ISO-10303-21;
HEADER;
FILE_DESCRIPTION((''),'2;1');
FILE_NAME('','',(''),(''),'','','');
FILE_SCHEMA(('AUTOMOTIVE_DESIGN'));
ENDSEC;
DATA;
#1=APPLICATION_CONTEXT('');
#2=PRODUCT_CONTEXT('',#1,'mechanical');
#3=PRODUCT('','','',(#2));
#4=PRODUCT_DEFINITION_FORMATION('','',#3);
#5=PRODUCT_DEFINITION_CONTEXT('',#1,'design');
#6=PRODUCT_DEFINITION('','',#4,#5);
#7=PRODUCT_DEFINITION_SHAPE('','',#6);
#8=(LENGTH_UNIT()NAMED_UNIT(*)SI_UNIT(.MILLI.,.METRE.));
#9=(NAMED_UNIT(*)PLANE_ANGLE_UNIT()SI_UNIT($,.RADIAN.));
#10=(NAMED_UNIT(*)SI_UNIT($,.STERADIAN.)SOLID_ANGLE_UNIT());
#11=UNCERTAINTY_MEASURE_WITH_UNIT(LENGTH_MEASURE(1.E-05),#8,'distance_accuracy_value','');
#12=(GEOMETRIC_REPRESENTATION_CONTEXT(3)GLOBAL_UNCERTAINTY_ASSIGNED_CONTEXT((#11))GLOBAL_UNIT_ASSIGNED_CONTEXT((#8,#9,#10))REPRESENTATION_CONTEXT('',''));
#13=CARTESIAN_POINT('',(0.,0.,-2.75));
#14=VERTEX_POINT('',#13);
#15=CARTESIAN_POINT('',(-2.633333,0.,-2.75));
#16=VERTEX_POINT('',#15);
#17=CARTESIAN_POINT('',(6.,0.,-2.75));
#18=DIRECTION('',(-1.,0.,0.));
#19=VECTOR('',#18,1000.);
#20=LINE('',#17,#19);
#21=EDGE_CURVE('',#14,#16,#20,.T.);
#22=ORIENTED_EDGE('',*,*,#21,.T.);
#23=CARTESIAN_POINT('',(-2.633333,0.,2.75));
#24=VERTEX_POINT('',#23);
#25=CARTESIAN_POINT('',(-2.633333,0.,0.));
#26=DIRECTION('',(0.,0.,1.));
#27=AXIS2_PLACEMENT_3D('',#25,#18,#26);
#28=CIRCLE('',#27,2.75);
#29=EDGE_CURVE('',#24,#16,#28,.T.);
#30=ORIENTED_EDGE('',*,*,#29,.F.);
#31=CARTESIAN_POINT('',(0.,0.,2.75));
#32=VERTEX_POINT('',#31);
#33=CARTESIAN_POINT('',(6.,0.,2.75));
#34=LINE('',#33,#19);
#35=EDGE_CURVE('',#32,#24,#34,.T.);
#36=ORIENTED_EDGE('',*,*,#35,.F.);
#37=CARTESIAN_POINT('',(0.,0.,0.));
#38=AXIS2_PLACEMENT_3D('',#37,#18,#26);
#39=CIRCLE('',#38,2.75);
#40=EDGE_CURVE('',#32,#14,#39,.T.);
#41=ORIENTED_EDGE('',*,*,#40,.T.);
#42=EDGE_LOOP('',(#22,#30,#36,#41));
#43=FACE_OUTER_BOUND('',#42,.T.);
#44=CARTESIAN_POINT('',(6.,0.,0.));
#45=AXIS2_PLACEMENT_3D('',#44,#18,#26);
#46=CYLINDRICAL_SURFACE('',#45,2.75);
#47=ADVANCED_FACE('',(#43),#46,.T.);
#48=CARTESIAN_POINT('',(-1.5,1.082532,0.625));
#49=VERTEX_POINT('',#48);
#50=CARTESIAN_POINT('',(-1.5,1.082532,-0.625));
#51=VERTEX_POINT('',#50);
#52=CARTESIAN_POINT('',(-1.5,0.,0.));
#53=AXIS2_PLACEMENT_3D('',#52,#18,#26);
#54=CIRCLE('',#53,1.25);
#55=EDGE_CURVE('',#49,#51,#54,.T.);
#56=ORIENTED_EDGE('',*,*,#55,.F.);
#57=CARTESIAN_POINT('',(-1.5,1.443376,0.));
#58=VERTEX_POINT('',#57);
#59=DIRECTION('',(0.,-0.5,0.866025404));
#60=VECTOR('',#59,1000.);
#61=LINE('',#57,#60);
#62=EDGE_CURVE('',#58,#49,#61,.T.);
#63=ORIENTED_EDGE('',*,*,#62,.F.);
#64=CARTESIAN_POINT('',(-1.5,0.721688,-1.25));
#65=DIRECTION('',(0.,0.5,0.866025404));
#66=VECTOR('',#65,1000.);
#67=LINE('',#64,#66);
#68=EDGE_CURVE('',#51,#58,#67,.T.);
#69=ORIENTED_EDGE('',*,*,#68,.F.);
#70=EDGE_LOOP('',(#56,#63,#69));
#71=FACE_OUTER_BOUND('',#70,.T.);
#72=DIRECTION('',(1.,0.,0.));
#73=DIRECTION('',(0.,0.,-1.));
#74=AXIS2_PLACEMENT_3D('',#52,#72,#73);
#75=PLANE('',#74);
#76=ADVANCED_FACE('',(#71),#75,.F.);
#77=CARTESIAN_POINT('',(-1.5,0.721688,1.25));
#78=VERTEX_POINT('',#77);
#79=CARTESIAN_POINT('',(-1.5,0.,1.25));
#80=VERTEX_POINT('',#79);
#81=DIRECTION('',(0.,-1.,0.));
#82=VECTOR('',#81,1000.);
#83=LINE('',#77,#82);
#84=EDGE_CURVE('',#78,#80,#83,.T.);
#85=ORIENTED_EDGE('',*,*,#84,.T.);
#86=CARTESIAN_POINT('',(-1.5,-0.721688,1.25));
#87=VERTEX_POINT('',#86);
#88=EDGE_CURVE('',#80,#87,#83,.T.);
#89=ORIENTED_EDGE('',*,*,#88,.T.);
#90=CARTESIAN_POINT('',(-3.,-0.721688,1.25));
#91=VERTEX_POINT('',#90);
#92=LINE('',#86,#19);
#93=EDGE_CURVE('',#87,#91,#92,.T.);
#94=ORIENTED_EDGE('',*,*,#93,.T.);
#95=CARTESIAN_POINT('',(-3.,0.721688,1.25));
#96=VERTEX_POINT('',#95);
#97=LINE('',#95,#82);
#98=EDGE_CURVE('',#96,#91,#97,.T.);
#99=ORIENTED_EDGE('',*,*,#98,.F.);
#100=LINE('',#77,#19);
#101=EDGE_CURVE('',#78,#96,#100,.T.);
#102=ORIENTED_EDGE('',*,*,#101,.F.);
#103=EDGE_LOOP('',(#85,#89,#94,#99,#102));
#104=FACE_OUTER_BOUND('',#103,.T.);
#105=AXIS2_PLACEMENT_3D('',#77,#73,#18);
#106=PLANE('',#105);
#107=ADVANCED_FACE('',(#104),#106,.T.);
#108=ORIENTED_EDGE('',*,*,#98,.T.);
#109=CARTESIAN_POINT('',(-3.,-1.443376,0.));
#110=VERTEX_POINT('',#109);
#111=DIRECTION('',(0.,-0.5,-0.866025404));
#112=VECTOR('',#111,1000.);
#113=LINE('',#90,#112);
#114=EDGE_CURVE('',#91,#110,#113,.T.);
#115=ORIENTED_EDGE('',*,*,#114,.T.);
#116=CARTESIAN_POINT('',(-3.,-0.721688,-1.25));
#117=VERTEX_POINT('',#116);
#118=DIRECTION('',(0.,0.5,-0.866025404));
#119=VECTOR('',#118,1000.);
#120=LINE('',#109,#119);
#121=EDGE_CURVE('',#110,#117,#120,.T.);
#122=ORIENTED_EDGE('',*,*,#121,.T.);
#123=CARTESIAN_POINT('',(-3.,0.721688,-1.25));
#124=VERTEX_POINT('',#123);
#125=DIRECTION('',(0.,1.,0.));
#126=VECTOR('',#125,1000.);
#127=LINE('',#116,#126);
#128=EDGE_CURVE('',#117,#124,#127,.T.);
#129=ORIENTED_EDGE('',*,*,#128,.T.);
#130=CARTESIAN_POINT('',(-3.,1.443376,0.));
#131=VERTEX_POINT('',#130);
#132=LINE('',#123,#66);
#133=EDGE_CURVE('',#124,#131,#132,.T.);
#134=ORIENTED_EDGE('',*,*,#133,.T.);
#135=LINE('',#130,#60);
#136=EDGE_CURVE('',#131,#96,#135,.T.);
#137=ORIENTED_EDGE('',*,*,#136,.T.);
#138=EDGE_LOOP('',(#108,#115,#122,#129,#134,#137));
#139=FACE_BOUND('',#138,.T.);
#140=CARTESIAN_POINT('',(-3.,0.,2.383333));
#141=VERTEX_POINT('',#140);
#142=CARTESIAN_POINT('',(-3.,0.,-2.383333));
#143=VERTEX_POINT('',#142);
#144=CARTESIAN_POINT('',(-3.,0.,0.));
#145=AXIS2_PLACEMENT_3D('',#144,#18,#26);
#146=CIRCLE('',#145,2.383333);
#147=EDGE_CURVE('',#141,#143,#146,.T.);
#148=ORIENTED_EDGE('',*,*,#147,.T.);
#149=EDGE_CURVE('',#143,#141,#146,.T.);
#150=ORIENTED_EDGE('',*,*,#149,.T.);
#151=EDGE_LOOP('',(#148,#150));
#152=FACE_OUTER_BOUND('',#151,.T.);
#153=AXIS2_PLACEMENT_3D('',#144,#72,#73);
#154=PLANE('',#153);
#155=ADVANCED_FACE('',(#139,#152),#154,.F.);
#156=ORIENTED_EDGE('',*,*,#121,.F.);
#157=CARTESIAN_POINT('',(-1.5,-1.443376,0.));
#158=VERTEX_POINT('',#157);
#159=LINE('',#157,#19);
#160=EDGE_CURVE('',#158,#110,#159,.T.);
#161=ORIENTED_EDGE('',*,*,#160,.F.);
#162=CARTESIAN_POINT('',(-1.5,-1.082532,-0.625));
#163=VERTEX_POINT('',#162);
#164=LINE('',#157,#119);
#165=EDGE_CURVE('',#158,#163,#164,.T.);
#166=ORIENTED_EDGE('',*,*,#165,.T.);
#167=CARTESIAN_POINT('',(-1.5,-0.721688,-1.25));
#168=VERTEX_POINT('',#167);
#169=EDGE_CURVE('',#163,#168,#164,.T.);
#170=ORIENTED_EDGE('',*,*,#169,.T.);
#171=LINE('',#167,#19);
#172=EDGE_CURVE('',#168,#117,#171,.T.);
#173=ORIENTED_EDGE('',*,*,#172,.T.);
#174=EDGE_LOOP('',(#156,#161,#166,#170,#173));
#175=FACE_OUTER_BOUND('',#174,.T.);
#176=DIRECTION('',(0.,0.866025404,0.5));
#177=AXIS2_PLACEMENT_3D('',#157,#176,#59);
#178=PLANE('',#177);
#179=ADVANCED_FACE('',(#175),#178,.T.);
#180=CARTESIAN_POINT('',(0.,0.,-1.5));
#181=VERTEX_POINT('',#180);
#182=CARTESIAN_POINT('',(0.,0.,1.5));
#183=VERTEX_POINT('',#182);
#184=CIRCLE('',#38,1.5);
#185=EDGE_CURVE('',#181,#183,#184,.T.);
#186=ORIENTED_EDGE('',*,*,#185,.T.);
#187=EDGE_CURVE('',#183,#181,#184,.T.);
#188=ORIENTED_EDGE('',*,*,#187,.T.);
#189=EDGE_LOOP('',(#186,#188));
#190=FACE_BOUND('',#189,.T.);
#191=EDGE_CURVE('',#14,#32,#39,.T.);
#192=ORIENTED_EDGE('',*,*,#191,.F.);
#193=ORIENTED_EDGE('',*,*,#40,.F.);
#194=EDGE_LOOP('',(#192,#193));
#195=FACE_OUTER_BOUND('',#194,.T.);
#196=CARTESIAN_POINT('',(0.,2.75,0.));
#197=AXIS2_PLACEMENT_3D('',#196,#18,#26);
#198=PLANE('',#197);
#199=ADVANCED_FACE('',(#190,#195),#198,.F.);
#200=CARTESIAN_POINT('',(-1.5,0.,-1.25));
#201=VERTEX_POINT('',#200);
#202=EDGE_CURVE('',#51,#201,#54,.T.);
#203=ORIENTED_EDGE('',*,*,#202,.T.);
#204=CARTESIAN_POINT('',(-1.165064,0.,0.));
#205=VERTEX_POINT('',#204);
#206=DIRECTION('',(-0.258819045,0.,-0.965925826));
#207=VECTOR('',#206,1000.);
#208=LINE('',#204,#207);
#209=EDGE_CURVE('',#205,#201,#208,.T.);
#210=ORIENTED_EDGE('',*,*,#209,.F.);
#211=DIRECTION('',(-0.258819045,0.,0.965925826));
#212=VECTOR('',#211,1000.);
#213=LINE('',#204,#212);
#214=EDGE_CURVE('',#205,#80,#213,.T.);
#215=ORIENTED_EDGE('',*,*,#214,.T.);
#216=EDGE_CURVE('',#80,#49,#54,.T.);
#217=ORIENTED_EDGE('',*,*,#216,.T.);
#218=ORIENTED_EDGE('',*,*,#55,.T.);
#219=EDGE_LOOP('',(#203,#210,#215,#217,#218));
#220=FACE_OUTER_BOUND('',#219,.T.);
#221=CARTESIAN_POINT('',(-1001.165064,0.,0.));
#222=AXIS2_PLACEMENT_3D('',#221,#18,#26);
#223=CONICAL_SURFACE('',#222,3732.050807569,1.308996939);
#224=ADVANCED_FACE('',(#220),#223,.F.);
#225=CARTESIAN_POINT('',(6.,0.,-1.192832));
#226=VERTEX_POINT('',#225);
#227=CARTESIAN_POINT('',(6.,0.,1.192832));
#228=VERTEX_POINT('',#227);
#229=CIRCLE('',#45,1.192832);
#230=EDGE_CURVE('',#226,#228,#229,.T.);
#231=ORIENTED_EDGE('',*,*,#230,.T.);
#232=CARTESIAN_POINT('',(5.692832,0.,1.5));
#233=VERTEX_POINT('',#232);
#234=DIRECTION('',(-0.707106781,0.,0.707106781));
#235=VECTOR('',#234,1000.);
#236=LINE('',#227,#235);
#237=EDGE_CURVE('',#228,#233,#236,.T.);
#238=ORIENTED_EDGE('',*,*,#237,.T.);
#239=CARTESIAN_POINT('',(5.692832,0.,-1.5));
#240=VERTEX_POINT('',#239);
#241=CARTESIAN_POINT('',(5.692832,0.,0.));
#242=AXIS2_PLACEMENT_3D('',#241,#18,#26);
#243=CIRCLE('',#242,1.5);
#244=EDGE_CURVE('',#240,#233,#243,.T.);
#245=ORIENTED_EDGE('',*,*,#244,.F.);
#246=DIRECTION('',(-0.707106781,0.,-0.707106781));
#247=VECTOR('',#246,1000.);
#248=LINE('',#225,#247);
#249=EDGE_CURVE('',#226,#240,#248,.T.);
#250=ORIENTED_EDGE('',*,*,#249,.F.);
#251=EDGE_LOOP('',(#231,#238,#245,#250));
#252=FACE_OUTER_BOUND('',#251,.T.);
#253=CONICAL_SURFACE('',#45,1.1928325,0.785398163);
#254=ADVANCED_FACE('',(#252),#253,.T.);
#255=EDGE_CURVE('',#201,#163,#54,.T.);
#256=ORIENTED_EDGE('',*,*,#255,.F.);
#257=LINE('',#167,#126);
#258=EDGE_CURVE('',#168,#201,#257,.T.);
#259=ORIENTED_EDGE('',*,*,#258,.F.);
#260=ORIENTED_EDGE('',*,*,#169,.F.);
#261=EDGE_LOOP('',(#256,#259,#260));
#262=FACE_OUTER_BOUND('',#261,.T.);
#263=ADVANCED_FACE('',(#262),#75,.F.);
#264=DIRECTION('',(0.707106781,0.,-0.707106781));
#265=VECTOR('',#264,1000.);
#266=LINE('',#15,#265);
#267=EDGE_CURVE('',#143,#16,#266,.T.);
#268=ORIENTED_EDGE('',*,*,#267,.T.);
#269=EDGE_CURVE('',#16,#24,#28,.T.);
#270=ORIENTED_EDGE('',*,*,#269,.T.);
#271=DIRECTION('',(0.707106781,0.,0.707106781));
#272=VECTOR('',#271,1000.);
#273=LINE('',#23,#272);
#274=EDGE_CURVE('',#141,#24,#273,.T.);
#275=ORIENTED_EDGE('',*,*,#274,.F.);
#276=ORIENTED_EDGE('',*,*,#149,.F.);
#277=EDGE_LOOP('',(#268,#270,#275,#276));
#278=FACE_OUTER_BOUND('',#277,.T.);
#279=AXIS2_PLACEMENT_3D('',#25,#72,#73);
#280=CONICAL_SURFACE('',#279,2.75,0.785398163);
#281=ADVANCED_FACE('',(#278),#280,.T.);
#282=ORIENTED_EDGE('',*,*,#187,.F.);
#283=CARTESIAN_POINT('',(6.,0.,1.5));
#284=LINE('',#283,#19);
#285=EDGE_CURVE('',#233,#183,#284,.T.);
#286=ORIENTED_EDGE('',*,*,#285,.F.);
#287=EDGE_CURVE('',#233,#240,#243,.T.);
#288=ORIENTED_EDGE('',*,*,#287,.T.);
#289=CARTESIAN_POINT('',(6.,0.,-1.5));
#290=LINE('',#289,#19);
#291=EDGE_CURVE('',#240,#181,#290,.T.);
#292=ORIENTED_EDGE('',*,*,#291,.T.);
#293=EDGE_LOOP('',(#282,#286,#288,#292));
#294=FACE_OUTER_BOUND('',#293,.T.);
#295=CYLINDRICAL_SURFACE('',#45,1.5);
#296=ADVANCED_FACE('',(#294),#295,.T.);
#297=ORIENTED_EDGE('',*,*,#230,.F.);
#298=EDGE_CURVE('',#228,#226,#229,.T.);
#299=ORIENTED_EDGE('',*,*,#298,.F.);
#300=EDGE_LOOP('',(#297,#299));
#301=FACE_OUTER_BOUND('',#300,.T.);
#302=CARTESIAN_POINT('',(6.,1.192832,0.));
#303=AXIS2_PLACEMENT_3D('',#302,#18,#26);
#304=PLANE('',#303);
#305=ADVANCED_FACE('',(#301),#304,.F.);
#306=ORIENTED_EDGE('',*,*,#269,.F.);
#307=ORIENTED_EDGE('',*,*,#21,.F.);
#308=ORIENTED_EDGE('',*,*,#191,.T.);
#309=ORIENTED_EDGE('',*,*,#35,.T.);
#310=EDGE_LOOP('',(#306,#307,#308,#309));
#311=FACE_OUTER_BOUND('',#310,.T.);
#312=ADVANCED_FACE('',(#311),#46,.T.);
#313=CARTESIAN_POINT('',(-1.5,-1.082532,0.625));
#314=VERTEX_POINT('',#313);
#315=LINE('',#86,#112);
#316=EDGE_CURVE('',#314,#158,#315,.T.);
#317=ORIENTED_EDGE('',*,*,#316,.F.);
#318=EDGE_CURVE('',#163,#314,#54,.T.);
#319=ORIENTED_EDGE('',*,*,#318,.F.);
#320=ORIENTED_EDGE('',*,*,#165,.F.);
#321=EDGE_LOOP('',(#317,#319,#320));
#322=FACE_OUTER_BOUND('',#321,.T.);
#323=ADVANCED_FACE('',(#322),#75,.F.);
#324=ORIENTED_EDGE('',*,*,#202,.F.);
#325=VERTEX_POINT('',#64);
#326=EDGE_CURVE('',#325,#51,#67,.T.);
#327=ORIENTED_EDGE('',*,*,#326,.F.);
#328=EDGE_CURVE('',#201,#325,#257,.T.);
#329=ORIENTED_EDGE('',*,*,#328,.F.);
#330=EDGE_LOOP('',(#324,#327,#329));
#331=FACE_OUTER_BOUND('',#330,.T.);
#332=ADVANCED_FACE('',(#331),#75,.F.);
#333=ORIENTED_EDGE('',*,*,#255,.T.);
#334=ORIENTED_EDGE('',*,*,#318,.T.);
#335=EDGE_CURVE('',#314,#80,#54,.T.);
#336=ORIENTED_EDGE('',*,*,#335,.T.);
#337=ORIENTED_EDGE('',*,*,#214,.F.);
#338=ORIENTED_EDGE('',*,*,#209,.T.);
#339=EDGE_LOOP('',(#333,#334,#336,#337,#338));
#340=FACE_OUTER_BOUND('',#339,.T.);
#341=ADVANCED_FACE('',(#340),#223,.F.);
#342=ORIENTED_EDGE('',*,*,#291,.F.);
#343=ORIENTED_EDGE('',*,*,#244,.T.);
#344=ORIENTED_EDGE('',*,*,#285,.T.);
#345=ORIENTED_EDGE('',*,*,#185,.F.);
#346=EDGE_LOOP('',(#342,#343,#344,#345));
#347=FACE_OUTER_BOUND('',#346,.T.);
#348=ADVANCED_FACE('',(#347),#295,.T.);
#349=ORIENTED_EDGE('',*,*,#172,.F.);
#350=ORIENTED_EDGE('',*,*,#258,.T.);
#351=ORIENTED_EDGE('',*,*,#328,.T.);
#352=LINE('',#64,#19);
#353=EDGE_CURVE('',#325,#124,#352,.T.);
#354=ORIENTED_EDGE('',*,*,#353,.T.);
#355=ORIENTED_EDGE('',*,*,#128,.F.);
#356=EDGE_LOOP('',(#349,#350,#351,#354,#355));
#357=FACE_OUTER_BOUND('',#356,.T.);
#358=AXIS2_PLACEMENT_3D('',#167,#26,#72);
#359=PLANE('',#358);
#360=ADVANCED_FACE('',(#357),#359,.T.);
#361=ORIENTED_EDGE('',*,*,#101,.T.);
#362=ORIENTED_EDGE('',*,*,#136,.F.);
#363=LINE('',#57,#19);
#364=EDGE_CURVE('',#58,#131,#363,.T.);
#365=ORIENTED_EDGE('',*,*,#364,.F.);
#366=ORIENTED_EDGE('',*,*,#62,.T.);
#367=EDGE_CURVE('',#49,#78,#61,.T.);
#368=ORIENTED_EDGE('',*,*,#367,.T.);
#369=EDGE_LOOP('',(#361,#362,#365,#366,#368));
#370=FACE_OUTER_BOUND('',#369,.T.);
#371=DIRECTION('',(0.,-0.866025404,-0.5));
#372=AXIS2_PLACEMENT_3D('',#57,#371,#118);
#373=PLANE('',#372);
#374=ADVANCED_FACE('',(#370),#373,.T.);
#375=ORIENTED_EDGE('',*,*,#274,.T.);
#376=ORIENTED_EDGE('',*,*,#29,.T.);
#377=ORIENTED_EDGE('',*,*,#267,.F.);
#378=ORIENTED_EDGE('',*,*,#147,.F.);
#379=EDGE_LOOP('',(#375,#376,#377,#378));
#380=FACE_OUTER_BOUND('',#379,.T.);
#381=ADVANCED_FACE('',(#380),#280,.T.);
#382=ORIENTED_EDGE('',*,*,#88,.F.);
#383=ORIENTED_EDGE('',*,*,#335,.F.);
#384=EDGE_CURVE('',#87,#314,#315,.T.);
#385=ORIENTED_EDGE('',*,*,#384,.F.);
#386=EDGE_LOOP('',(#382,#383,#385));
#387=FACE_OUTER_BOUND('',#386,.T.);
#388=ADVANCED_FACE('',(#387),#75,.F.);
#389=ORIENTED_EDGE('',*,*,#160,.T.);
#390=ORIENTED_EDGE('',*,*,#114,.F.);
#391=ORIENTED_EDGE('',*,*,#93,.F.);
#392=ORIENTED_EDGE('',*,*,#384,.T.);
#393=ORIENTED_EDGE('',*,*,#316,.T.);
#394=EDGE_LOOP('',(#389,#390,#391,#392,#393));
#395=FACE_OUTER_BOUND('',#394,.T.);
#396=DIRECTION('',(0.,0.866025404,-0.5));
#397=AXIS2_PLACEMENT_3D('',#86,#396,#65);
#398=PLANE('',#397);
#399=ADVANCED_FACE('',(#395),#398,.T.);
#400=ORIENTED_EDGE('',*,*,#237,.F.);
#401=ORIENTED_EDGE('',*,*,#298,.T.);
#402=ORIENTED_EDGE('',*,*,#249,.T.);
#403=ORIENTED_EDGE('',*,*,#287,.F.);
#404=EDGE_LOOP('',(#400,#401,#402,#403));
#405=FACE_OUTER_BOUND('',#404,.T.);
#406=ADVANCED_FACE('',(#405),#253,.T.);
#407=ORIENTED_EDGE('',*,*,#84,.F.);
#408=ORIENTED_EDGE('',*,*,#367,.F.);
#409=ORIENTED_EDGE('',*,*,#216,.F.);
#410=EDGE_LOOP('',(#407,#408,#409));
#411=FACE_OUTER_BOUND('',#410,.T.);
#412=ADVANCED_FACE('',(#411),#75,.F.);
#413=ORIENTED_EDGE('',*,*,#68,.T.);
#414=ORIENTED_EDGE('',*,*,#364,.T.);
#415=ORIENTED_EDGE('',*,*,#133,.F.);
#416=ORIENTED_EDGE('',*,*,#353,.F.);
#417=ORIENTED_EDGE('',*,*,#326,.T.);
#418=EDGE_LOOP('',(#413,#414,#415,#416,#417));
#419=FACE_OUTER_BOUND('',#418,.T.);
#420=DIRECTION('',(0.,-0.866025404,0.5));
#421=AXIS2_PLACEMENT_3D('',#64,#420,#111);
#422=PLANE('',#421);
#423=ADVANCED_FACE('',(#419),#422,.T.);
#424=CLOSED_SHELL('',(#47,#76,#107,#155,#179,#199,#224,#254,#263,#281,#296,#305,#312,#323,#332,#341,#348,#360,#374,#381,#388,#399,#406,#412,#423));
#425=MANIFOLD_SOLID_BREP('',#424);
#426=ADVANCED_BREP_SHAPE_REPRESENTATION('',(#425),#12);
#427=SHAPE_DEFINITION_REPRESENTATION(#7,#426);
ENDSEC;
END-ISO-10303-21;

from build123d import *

# Parameters (mm, degrees)
CUT_EXTRUDE1_DEPTH = 1.5


with BuildPart() as part:
    # Sketch1 → Revolve1 (revolve)
    with BuildSketch(Plane.XY, mode=Mode.PRIVATE) as revolve1_sk:
        Polygon((-3, 0), (-3, 2.383333333), (-2.633333333, 2.75), (0, 2.75), (0, 1.5), (5.6928325, 1.5), (6, 1.1928325), (6, 0), align=None)
    revolve(revolve1_sk.sketch.rotate(Axis((6, 0, 0), (-1, 0, 0)), 270), axis=Axis((6, 0, 0), (-1, 0, 0)))

    # Sketch2 → Cut-Revolve1 (revolve, cut)
    with BuildSketch(Plane.XY, mode=Mode.PRIVATE) as cut_revolve1_sk:
        Polygon((-3, 0), (-3, 1.25), (-1.5, 1.25), (-1.165063509, 0), align=None)
    revolve(cut_revolve1_sk.sketch.rotate(Axis((-1.165063509, 0, 0), (-1, 0, 0)), 270), axis=Axis((-1.165063509, 0, 0), (-1, 0, 0)), mode=Mode.SUBTRACT)

    # Sketch3 → Cut-Extrude1 (cut)
    with BuildSketch(Plane(origin=(-3, 0, 0), x_dir=(0, 0, -1), z_dir=(1, 0, 0))):
        Polygon((-1.25, 0.721687836), (-1.25, -0.721687836), (0, -1.443375673), (1.25, -0.721687836), (1.25, 0.721687836), (0, 1.443375673), align=None)
    extrude(amount=CUT_EXTRUDE1_DEPTH, mode=Mode.SUBTRACT)


solid = part.part
